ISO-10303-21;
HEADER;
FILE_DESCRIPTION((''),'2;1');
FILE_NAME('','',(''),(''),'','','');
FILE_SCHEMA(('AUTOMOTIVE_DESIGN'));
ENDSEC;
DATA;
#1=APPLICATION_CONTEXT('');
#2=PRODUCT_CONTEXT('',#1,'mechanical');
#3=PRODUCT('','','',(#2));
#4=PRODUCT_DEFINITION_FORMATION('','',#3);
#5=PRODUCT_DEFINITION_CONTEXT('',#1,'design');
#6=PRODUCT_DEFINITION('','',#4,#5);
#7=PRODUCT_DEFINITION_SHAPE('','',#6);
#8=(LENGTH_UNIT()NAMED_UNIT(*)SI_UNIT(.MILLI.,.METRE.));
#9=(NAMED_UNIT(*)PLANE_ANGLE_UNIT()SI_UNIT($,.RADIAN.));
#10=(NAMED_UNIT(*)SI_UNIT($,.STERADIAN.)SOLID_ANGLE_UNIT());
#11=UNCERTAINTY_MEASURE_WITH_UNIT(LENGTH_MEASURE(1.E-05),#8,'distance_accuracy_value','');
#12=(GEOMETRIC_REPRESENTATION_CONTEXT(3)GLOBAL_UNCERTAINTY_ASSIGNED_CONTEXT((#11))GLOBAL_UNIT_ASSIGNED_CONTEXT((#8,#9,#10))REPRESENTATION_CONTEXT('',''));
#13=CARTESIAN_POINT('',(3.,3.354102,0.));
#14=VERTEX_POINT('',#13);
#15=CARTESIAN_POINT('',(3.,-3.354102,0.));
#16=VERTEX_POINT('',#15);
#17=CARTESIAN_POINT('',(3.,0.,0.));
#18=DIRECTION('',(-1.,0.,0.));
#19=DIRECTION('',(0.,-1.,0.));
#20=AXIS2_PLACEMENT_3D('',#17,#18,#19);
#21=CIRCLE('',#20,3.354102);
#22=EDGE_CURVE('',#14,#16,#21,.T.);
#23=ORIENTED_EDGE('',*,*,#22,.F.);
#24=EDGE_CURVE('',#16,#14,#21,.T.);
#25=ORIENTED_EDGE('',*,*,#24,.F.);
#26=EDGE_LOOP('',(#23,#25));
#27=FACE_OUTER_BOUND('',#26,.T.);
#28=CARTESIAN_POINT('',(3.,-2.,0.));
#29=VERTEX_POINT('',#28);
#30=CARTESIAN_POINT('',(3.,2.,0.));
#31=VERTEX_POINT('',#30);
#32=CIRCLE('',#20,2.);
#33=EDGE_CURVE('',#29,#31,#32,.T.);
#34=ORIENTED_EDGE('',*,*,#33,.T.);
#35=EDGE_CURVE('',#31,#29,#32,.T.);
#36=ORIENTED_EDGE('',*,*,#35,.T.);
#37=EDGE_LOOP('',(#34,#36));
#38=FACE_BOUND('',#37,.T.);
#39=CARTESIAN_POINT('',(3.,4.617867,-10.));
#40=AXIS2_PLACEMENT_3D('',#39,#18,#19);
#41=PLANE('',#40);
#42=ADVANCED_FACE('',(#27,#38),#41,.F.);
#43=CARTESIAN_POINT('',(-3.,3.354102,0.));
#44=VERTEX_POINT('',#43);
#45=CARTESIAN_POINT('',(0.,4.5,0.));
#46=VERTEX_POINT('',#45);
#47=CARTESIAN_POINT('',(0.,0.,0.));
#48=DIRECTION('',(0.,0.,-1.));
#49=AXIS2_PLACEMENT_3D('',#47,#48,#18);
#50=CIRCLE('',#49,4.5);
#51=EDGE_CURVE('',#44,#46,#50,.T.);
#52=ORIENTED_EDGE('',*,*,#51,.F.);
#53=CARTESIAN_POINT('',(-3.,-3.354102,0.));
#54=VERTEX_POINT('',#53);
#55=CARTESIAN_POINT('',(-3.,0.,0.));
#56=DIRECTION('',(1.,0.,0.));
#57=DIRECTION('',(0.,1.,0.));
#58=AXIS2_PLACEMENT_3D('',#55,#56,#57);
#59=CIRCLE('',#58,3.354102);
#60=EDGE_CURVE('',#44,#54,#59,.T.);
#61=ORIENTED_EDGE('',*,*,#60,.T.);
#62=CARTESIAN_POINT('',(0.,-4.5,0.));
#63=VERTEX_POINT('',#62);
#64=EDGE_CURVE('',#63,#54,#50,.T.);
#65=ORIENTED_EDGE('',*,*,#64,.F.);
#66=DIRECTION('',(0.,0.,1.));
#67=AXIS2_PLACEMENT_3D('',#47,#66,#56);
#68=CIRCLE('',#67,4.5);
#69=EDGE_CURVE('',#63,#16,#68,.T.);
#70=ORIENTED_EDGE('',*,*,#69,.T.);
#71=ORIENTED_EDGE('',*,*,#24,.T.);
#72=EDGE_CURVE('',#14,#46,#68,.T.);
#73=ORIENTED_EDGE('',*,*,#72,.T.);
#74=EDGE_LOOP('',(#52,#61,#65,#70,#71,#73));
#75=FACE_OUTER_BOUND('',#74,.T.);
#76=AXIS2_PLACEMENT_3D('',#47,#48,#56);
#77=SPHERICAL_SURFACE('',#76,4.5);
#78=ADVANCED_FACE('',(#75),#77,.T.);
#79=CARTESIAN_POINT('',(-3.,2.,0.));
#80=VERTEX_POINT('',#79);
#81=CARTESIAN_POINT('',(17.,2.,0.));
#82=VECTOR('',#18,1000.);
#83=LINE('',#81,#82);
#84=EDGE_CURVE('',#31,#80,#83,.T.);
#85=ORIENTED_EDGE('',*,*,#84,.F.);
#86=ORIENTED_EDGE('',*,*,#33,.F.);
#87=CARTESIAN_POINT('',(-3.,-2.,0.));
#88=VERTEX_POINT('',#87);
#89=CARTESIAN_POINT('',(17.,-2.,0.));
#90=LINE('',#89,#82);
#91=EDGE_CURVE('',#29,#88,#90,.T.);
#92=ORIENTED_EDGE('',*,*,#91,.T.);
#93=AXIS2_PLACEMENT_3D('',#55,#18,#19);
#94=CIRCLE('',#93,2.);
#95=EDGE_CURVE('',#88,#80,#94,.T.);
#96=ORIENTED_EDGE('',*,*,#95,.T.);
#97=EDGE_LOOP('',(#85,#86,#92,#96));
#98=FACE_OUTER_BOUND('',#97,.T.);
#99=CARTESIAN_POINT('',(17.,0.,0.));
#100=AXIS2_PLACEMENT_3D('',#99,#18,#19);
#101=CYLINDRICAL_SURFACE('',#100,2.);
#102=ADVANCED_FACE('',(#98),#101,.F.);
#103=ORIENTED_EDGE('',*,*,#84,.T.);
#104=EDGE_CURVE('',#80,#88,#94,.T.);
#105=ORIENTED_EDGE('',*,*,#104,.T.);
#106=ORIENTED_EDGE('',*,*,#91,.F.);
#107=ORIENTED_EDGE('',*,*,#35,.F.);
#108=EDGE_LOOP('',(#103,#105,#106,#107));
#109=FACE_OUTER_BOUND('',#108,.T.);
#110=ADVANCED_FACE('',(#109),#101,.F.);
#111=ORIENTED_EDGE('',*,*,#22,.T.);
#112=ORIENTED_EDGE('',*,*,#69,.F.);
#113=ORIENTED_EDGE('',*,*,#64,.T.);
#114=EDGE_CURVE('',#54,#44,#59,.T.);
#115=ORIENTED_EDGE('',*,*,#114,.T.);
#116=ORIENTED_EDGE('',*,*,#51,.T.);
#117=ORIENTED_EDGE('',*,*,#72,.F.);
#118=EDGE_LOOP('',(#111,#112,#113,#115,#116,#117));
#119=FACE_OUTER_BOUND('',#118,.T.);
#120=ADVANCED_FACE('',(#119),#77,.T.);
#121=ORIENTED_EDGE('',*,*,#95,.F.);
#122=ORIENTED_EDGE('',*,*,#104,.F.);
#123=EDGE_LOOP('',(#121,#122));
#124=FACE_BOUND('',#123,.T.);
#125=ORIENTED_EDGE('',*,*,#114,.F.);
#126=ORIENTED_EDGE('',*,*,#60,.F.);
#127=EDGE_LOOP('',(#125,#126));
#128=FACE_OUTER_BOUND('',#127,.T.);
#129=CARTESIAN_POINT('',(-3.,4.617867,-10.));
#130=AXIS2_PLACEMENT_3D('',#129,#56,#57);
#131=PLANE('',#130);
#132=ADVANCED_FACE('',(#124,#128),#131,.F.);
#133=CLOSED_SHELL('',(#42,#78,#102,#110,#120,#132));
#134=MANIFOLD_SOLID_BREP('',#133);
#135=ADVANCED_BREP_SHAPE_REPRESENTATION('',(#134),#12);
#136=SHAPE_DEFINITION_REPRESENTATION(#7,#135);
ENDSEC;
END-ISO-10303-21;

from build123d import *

# Parameters (mm, degrees)
SKETCH4_W          = 4.737450542
SKETCH4_H          = 9.271952016
CUT_EXTRUDE2_DEPTH = 10
SKETCH5_R          = 2
CUT_EXTRUDE3_DEPTH = 20


with BuildPart() as part:
    # Sketch1 → Revolve4 (revolve)
    with BuildSketch(Plane.XY):
        with BuildLine():
            Line((0, 4.5), (0, -4.5))
            ThreePointArc((0, -4.5), (4.5, 0), (0, 4.5))
        make_face()
    revolve(axis=Axis((0, 4.5, 0), (0, -1, 0)))

    # Sketch4 → Cut-Extrude2 (cut, symmetric)
    with BuildSketch(Plane.XY):
        with Locations((5.368725271, -0.018109281)):
            Rectangle(SKETCH4_W, SKETCH4_H)
        with Locations((-5.368725271, -0.018109281)):
            Rectangle(SKETCH4_W, SKETCH4_H)
    extrude(amount=CUT_EXTRUDE2_DEPTH, both=True, mode=Mode.SUBTRACT)

    # Sketch5 → Cut-Extrude3 (cut)
    with BuildSketch(Plane.ZY.offset(3)):
        with Locations(Location((0, 0, 0), (0, 0, 270))):
            Circle(SKETCH5_R)
    extrude(amount=-CUT_EXTRUDE3_DEPTH, mode=Mode.SUBTRACT)


solid = part.part
